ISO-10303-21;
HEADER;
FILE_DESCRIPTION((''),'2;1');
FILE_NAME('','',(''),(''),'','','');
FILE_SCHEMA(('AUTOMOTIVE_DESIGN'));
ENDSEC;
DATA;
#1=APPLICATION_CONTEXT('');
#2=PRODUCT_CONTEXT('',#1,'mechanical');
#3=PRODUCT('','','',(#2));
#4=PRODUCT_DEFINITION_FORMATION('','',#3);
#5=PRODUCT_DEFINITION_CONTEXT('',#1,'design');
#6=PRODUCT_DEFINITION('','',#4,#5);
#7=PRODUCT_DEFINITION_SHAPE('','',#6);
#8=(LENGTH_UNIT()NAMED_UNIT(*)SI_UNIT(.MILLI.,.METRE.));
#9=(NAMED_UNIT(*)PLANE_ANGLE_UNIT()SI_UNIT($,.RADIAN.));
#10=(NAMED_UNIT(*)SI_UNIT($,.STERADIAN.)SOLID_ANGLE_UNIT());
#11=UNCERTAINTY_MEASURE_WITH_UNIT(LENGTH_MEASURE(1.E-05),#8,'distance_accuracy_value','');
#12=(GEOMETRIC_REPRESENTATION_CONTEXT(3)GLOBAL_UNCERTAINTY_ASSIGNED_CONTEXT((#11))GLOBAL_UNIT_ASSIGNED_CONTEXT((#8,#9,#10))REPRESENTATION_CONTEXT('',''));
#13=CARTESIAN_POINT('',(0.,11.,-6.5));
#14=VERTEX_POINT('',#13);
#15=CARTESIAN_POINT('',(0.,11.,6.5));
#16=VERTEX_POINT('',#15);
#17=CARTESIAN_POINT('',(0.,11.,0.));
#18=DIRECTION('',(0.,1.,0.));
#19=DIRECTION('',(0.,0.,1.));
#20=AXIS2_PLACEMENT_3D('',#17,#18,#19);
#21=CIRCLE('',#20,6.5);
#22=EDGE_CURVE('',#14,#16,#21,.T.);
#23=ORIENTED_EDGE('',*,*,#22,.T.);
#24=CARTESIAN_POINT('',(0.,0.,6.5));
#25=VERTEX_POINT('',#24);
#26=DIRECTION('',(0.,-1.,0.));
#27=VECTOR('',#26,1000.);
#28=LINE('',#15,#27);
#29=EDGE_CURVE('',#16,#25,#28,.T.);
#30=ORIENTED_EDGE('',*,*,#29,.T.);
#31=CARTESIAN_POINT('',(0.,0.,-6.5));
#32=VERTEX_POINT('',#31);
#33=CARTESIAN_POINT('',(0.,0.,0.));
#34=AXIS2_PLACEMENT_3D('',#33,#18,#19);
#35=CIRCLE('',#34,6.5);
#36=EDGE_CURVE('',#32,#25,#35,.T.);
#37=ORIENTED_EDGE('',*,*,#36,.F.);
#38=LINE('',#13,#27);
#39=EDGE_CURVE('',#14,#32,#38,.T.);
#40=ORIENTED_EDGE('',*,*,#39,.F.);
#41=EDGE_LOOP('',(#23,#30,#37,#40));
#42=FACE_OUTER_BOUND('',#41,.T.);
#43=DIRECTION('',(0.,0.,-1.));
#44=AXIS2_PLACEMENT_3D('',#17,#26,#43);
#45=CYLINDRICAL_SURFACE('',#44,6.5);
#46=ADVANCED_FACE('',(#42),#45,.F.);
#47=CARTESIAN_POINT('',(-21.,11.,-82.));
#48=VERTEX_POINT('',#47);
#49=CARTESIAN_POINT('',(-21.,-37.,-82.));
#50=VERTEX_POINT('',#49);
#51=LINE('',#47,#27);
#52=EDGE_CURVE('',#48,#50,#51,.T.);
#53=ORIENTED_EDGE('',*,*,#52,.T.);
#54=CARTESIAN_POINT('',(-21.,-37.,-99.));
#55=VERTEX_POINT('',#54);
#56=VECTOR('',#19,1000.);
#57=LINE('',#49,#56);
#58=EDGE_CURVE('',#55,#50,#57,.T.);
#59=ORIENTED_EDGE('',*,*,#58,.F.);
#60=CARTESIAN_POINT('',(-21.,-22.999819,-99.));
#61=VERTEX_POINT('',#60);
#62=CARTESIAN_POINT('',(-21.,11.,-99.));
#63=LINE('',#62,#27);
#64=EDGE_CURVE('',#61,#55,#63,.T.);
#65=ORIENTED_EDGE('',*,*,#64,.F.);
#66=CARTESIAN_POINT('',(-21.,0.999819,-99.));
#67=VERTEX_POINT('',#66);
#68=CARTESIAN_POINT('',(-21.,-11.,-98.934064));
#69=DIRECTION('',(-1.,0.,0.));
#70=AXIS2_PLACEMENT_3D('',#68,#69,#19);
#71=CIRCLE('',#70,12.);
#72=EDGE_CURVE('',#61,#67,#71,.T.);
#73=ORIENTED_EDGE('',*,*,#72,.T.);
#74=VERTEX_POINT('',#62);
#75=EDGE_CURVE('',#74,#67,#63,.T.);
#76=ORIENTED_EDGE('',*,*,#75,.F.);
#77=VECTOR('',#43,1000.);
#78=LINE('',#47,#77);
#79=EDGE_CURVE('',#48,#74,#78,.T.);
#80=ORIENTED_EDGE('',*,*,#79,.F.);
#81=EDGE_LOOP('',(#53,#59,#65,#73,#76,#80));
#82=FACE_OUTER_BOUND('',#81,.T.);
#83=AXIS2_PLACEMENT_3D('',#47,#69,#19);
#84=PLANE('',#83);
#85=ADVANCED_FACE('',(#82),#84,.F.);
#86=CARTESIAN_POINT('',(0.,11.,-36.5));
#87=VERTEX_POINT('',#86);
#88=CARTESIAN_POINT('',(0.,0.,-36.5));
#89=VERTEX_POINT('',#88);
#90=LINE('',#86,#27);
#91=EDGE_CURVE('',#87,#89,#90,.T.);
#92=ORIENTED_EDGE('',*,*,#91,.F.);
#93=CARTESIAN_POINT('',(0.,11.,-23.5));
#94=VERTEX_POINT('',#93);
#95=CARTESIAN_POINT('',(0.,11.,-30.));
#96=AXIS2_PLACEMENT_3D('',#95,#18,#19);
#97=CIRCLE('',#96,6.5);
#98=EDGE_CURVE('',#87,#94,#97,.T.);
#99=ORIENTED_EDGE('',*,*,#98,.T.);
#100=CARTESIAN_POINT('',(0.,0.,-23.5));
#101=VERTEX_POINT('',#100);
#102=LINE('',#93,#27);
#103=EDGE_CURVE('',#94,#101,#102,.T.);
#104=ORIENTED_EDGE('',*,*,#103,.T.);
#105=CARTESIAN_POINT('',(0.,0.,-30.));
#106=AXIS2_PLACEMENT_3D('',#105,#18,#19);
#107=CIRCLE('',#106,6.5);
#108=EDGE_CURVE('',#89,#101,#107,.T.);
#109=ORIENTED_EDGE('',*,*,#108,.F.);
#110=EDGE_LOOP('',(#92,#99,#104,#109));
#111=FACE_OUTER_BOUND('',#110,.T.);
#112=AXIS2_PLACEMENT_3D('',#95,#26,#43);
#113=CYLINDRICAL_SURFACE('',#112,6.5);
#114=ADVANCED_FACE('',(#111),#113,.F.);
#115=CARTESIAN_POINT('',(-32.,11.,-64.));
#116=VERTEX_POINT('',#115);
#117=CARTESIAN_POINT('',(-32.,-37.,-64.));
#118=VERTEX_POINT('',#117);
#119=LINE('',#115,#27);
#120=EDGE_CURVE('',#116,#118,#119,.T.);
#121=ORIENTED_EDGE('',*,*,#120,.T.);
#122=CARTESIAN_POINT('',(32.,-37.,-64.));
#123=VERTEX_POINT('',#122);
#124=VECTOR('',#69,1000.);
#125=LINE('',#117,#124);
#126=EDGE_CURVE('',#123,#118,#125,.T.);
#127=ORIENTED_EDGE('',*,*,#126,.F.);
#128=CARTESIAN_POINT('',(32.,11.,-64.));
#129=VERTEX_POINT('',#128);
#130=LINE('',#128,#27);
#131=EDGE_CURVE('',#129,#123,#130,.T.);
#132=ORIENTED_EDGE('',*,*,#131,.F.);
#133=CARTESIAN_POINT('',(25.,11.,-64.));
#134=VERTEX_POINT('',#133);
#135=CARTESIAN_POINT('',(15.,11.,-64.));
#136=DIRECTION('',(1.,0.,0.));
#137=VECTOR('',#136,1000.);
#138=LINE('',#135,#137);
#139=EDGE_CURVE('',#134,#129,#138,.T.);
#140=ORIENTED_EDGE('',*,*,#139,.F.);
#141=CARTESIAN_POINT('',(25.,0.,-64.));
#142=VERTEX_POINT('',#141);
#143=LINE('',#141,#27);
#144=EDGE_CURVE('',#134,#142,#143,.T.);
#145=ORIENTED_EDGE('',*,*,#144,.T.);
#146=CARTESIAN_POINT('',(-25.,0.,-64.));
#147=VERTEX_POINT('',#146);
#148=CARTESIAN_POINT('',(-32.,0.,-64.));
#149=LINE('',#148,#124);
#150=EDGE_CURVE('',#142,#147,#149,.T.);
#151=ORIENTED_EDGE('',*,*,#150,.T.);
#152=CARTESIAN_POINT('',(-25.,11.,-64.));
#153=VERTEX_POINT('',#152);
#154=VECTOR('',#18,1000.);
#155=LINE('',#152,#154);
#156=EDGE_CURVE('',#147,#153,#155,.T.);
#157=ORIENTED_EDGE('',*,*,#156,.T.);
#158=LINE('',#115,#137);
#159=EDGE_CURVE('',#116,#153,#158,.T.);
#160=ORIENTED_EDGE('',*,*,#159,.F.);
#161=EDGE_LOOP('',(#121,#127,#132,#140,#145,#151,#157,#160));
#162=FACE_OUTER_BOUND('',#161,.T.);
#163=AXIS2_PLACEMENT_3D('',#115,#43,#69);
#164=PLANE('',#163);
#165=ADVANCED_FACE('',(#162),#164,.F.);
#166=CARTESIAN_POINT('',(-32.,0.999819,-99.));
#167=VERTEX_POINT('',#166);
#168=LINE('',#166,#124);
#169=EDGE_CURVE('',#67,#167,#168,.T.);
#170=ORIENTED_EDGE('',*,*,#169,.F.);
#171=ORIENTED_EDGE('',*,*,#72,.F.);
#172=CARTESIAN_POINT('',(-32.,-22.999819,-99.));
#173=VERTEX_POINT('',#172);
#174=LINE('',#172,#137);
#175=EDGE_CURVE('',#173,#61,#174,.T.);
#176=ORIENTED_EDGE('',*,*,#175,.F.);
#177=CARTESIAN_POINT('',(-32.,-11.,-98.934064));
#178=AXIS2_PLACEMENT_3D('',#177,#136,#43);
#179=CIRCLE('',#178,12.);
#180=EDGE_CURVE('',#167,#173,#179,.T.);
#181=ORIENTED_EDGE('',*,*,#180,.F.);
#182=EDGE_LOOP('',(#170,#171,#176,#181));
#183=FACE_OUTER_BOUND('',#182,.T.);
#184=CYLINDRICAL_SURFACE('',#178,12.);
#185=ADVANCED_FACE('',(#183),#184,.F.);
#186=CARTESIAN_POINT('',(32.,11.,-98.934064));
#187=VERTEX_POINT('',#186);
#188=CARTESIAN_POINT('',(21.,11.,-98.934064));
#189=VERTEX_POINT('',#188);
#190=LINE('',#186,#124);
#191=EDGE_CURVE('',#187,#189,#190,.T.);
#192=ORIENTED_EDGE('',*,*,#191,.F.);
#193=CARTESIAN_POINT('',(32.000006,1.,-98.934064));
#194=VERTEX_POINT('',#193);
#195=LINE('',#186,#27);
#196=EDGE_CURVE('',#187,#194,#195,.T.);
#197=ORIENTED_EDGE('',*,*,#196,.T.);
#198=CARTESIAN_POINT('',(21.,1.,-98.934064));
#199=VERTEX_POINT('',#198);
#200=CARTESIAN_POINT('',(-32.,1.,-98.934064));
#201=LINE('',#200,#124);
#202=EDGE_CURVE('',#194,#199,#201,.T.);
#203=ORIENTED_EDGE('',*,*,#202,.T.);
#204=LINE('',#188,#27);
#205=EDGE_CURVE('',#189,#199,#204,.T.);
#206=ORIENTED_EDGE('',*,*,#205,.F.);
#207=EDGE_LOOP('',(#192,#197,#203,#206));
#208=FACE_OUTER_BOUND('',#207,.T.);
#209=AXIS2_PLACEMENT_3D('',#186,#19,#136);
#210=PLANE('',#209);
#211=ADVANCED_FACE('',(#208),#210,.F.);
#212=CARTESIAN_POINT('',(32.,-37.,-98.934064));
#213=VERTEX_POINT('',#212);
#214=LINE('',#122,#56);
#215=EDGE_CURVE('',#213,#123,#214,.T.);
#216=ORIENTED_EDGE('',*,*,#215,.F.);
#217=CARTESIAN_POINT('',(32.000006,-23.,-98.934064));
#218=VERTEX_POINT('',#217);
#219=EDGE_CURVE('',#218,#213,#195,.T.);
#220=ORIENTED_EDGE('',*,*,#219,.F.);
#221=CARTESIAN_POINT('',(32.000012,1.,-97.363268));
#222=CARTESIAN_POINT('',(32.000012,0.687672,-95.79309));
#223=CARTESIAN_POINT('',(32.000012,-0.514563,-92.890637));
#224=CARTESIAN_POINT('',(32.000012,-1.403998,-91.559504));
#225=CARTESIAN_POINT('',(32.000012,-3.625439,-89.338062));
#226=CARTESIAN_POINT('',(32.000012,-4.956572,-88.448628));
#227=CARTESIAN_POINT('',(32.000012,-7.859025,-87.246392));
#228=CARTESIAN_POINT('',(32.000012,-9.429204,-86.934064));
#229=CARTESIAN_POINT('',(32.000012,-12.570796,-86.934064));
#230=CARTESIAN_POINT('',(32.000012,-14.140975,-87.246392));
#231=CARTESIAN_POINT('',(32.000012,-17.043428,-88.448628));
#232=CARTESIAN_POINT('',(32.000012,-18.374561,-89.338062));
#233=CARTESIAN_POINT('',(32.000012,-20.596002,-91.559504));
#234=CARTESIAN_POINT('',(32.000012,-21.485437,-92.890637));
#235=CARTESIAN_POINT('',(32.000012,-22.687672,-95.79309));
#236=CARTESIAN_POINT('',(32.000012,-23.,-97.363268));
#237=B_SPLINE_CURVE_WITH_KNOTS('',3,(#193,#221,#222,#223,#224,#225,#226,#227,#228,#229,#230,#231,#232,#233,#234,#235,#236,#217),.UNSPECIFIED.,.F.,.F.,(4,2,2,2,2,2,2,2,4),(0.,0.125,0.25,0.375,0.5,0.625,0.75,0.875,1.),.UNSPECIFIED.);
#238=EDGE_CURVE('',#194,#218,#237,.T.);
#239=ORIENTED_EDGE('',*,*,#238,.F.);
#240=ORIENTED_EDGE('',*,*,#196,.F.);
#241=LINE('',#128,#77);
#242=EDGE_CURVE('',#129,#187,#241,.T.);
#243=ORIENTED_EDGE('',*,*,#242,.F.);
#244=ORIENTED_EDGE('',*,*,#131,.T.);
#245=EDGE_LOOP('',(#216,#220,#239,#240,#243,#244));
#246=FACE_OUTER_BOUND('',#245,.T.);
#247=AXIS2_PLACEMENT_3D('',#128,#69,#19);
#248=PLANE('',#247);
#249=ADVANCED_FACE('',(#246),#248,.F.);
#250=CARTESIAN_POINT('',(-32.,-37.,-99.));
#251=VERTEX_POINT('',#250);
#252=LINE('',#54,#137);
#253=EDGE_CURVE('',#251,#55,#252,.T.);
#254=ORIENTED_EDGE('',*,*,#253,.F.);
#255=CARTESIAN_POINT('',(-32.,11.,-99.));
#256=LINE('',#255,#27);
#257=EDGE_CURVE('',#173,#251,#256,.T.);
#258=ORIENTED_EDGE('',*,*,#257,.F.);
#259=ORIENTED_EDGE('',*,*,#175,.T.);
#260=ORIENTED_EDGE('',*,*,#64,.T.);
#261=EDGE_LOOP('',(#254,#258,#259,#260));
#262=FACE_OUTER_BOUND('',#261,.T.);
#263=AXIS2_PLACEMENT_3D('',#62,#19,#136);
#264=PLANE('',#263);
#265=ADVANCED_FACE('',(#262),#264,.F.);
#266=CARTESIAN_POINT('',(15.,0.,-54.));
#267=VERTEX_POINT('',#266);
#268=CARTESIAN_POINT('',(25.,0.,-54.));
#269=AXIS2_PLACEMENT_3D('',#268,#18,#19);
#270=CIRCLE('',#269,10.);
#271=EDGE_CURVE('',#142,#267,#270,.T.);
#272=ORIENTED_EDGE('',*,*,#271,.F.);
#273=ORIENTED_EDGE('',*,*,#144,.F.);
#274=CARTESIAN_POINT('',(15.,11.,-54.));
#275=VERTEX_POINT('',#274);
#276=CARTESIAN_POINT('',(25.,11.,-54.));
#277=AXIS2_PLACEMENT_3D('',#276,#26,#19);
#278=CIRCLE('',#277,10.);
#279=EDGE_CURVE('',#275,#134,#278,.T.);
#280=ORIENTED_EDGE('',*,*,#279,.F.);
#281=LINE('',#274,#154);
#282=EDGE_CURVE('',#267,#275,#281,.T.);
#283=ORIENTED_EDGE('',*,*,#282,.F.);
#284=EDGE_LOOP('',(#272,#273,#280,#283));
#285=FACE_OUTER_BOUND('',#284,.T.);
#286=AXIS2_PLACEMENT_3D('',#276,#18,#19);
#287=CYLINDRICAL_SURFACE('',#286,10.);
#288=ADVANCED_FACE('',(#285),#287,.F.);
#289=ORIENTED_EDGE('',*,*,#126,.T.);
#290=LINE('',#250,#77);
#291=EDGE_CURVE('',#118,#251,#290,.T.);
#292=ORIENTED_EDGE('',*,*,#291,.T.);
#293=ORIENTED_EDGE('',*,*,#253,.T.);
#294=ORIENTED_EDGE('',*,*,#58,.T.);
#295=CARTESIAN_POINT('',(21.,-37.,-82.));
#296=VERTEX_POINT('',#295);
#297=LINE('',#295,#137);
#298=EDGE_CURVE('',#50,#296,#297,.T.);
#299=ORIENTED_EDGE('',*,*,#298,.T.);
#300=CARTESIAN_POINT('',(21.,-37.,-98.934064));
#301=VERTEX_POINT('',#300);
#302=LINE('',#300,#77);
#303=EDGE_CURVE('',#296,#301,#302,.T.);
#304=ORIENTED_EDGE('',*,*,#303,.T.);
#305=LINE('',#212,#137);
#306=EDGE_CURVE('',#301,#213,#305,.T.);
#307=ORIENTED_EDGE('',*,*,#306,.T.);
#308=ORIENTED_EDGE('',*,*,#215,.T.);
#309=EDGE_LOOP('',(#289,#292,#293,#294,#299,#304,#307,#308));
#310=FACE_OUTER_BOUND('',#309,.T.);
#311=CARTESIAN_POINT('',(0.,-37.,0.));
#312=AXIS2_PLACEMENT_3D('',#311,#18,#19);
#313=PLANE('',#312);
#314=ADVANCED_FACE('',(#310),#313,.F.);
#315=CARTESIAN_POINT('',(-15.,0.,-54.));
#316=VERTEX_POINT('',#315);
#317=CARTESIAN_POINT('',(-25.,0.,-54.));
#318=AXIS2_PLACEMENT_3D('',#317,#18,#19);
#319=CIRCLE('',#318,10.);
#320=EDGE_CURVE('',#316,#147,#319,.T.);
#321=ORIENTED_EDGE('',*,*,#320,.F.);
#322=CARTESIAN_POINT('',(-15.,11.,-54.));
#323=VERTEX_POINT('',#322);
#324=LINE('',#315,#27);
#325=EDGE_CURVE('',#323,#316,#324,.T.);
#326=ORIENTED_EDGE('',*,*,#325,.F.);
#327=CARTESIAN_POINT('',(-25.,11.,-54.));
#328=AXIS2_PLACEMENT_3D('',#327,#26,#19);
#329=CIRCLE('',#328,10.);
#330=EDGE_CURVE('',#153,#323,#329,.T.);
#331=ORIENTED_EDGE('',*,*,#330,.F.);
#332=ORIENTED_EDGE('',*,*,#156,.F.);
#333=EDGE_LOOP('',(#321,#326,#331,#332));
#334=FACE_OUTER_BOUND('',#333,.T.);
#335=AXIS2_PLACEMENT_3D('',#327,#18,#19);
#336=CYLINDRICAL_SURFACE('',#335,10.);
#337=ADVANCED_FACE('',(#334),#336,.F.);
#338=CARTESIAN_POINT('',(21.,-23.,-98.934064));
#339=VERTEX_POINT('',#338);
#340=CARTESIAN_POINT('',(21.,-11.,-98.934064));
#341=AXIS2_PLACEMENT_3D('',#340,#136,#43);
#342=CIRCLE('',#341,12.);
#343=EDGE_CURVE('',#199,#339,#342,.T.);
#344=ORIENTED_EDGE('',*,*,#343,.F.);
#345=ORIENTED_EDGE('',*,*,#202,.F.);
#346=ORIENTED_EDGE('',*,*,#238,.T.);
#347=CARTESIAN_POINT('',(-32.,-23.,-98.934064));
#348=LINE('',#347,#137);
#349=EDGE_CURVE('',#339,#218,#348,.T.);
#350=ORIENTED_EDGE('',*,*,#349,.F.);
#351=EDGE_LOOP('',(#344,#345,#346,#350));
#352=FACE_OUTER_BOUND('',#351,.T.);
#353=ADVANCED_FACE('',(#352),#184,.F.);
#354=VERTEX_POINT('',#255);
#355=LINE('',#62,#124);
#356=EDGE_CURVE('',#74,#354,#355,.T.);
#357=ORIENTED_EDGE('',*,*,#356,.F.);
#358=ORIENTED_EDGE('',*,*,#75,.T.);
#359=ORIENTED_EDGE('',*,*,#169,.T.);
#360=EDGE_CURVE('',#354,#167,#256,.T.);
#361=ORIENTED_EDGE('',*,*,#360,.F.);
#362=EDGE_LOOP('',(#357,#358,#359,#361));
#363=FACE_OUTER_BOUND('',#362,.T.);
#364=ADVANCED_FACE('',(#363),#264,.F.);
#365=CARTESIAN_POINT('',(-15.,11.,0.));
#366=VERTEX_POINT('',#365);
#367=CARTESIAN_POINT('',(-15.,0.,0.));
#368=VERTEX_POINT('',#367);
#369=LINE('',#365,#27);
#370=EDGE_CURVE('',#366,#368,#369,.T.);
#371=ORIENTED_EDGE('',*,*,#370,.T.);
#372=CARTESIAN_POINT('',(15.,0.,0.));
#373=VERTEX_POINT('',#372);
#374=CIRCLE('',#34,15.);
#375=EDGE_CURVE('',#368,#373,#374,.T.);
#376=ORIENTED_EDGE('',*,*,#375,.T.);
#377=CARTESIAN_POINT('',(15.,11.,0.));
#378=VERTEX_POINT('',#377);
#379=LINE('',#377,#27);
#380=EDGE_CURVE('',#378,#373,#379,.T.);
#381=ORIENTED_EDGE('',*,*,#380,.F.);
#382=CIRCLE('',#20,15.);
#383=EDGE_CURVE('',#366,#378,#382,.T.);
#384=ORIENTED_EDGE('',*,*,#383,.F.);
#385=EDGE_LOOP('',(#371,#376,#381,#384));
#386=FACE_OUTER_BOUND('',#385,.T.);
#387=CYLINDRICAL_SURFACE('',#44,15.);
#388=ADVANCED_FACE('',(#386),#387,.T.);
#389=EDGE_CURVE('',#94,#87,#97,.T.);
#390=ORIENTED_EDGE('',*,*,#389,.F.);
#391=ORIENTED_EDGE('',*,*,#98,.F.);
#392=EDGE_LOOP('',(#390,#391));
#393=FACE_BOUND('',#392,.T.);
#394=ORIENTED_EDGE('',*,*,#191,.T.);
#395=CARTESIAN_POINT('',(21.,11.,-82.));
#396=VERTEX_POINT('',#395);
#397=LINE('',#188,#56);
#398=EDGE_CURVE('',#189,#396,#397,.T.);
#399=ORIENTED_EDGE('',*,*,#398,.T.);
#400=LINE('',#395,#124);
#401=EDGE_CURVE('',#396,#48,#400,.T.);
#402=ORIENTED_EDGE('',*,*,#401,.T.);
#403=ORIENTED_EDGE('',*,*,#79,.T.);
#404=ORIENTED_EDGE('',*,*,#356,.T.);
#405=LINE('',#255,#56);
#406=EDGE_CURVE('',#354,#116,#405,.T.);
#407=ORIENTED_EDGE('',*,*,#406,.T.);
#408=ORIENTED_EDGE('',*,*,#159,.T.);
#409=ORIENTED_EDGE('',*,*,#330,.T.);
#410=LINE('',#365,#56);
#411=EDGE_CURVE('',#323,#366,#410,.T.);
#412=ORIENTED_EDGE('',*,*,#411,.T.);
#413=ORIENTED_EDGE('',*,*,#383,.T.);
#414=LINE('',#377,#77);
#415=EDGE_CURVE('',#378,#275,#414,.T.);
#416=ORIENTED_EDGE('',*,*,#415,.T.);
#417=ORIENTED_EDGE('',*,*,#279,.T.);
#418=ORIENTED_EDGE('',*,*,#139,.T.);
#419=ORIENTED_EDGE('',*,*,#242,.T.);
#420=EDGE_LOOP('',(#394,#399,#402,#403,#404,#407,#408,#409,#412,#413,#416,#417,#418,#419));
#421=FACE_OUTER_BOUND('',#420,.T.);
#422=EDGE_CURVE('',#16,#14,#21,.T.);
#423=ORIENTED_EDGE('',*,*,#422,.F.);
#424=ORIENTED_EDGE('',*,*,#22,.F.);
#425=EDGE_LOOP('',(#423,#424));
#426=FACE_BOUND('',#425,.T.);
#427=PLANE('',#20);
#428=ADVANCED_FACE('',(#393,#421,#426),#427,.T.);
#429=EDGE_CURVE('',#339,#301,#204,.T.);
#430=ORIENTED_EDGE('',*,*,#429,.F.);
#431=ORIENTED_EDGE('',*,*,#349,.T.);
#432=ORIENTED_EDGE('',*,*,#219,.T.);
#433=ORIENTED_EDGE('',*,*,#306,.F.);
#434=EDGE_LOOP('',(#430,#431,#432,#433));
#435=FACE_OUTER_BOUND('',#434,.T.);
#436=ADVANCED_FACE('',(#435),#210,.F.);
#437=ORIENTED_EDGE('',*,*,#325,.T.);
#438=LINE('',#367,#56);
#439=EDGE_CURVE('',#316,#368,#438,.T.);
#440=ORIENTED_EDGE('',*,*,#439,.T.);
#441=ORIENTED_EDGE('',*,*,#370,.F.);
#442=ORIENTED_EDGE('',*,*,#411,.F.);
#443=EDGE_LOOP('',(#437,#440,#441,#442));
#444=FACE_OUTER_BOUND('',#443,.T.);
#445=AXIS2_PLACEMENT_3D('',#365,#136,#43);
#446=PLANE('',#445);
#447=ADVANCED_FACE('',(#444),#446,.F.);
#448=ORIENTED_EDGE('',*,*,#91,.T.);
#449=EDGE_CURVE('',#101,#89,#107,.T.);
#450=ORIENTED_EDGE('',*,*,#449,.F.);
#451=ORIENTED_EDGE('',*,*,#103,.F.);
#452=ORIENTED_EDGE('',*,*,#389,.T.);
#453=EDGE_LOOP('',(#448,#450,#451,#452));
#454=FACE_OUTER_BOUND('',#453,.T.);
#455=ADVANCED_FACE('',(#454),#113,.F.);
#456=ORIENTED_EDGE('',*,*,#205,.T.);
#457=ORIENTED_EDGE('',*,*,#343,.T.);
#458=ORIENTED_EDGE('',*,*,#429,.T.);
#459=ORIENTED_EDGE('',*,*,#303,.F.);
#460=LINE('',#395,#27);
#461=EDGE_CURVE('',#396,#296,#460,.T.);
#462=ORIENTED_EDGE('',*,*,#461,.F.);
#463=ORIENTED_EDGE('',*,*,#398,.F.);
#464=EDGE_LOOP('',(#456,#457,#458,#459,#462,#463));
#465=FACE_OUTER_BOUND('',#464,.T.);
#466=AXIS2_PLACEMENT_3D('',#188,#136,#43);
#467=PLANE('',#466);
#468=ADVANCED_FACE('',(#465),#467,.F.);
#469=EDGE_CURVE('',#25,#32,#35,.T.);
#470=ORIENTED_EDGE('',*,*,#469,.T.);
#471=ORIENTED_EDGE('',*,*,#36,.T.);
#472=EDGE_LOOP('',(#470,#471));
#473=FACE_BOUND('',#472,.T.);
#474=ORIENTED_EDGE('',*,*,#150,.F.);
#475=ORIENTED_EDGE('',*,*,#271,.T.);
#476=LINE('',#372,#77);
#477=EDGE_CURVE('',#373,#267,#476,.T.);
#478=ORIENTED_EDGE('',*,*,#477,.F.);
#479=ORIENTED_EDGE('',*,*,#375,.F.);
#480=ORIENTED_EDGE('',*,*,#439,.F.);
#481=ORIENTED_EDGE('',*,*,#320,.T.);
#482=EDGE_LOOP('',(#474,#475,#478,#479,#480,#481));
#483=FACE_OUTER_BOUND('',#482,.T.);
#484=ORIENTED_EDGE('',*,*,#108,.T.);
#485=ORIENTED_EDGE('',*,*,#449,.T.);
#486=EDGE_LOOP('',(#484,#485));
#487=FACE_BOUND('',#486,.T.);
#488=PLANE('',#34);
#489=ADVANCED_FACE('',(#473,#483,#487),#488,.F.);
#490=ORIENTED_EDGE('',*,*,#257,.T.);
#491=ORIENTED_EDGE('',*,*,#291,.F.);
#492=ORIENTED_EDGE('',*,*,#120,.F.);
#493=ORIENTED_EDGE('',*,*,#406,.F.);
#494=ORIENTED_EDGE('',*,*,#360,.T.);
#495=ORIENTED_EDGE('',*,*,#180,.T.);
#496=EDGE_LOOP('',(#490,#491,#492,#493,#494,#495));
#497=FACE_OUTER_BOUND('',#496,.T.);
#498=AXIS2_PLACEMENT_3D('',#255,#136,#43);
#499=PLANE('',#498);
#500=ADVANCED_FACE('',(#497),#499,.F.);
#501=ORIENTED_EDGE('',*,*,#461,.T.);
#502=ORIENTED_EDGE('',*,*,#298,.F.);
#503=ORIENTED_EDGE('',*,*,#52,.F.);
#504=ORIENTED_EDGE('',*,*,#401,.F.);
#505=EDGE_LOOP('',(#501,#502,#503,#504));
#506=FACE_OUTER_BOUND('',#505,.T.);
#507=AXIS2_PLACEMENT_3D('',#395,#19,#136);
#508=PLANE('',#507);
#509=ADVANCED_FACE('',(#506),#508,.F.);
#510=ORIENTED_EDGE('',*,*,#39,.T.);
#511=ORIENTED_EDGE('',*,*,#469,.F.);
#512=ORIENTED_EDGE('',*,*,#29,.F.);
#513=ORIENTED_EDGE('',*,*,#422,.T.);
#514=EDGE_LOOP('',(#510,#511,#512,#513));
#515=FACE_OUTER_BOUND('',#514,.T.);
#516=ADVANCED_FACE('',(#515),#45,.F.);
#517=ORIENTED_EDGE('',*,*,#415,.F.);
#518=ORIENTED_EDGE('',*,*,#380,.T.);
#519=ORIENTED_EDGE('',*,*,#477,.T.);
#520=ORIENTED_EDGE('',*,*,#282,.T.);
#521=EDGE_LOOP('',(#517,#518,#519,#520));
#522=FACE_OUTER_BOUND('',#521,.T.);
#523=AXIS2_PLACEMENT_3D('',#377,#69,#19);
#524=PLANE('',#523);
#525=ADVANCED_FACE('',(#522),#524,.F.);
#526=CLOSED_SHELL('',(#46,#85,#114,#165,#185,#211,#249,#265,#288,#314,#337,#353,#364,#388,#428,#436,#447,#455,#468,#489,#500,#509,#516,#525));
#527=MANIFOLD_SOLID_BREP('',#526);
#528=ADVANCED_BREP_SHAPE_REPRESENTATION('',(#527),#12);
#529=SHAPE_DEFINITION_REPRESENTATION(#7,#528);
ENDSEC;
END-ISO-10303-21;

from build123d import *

# Parameters (mm, degrees)
PLATE_PROFILE_SKETCH_R    = 6.5
MOUNTING_PLATE_11MM_DEPTH = 11
SUPPORT_BLOCK_37MM_DEPTH  = 37
FILLET_R10_R              = 10
ARM_HOLE_DEPTH            = 124.555655476
ARM_HOLE_DEPTH_BACK       = 124.555655476
ARM_HOLE_SKETCH_R         = 12


with BuildPart() as part:
    # Plate Profile Sketch → Mounting Plate 11mm (new body)
    with BuildSketch(Plane(origin=(0, 0, 0), x_dir=(1, 0, 0), z_dir=(0, 1, 0))):
        with BuildLine():
            Line((-15, 0), (-15, 64))
            Line((-15, 64), (-32, 64))
            Line((-32, 64), (-32, 99))
            Line((-32, 99), (-21, 99))
            Line((-21, 99), (-21, 82))
            Line((-21, 82), (21, 82))
            Line((21, 82), (21, 98.934064449))
            Line((21, 98.934064449), (32, 98.934064449))
            Line((32, 98.934064449), (32, 64))
            Line((32, 64), (15, 64))
            Line((15, 64), (15, 0))
            ThreePointArc((15, 0), (0, -15), (-15, 0))
        make_face()
        with Locations(Location((0, 0, 0), (0, 0, 270))):
            Circle(PLATE_PROFILE_SKETCH_R, mode=Mode.SUBTRACT)
        with Locations(Location((0, 30, 0), (0, 0, 270))):
            Circle(PLATE_PROFILE_SKETCH_R, mode=Mode.SUBTRACT)
    extrude(amount=MOUNTING_PLATE_11MM_DEPTH)

    # Support Block Sketch → Support Block 37mm (add)
    with BuildSketch(Plane.XZ):
        Polygon((-32, -64), (32, -64), (32, -98.934064449), (21, -98.934064449), (21, -82), (-21, -82), (-21, -99), (-32, -99), align=None)
    extrude(amount=SUPPORT_BLOCK_37MM_DEPTH)

    # Fillet R10
    fillet_r10_edges = [part.edges().sort_by_distance(p)[0] for p in [
        (-15, 5.5, -64),
        (15, 5.5, -64),
    ]]
    fillet(fillet_r10_edges, radius=FILLET_R10_R)

    # Arm Hole Sketch → Arm Hole (cut, two sides: drawn at the far end of the back side and taken through both)
    with BuildSketch(Plane(origin=(32, 0, 0), x_dir=(0, 0, -1), z_dir=(1, 0, 0)).offset(-ARM_HOLE_DEPTH_BACK)):
        with Locations((98.934064449, -11)):
            Circle(ARM_HOLE_SKETCH_R)
    extrude(amount=ARM_HOLE_DEPTH + ARM_HOLE_DEPTH_BACK, mode=Mode.SUBTRACT)


solid = part.part
